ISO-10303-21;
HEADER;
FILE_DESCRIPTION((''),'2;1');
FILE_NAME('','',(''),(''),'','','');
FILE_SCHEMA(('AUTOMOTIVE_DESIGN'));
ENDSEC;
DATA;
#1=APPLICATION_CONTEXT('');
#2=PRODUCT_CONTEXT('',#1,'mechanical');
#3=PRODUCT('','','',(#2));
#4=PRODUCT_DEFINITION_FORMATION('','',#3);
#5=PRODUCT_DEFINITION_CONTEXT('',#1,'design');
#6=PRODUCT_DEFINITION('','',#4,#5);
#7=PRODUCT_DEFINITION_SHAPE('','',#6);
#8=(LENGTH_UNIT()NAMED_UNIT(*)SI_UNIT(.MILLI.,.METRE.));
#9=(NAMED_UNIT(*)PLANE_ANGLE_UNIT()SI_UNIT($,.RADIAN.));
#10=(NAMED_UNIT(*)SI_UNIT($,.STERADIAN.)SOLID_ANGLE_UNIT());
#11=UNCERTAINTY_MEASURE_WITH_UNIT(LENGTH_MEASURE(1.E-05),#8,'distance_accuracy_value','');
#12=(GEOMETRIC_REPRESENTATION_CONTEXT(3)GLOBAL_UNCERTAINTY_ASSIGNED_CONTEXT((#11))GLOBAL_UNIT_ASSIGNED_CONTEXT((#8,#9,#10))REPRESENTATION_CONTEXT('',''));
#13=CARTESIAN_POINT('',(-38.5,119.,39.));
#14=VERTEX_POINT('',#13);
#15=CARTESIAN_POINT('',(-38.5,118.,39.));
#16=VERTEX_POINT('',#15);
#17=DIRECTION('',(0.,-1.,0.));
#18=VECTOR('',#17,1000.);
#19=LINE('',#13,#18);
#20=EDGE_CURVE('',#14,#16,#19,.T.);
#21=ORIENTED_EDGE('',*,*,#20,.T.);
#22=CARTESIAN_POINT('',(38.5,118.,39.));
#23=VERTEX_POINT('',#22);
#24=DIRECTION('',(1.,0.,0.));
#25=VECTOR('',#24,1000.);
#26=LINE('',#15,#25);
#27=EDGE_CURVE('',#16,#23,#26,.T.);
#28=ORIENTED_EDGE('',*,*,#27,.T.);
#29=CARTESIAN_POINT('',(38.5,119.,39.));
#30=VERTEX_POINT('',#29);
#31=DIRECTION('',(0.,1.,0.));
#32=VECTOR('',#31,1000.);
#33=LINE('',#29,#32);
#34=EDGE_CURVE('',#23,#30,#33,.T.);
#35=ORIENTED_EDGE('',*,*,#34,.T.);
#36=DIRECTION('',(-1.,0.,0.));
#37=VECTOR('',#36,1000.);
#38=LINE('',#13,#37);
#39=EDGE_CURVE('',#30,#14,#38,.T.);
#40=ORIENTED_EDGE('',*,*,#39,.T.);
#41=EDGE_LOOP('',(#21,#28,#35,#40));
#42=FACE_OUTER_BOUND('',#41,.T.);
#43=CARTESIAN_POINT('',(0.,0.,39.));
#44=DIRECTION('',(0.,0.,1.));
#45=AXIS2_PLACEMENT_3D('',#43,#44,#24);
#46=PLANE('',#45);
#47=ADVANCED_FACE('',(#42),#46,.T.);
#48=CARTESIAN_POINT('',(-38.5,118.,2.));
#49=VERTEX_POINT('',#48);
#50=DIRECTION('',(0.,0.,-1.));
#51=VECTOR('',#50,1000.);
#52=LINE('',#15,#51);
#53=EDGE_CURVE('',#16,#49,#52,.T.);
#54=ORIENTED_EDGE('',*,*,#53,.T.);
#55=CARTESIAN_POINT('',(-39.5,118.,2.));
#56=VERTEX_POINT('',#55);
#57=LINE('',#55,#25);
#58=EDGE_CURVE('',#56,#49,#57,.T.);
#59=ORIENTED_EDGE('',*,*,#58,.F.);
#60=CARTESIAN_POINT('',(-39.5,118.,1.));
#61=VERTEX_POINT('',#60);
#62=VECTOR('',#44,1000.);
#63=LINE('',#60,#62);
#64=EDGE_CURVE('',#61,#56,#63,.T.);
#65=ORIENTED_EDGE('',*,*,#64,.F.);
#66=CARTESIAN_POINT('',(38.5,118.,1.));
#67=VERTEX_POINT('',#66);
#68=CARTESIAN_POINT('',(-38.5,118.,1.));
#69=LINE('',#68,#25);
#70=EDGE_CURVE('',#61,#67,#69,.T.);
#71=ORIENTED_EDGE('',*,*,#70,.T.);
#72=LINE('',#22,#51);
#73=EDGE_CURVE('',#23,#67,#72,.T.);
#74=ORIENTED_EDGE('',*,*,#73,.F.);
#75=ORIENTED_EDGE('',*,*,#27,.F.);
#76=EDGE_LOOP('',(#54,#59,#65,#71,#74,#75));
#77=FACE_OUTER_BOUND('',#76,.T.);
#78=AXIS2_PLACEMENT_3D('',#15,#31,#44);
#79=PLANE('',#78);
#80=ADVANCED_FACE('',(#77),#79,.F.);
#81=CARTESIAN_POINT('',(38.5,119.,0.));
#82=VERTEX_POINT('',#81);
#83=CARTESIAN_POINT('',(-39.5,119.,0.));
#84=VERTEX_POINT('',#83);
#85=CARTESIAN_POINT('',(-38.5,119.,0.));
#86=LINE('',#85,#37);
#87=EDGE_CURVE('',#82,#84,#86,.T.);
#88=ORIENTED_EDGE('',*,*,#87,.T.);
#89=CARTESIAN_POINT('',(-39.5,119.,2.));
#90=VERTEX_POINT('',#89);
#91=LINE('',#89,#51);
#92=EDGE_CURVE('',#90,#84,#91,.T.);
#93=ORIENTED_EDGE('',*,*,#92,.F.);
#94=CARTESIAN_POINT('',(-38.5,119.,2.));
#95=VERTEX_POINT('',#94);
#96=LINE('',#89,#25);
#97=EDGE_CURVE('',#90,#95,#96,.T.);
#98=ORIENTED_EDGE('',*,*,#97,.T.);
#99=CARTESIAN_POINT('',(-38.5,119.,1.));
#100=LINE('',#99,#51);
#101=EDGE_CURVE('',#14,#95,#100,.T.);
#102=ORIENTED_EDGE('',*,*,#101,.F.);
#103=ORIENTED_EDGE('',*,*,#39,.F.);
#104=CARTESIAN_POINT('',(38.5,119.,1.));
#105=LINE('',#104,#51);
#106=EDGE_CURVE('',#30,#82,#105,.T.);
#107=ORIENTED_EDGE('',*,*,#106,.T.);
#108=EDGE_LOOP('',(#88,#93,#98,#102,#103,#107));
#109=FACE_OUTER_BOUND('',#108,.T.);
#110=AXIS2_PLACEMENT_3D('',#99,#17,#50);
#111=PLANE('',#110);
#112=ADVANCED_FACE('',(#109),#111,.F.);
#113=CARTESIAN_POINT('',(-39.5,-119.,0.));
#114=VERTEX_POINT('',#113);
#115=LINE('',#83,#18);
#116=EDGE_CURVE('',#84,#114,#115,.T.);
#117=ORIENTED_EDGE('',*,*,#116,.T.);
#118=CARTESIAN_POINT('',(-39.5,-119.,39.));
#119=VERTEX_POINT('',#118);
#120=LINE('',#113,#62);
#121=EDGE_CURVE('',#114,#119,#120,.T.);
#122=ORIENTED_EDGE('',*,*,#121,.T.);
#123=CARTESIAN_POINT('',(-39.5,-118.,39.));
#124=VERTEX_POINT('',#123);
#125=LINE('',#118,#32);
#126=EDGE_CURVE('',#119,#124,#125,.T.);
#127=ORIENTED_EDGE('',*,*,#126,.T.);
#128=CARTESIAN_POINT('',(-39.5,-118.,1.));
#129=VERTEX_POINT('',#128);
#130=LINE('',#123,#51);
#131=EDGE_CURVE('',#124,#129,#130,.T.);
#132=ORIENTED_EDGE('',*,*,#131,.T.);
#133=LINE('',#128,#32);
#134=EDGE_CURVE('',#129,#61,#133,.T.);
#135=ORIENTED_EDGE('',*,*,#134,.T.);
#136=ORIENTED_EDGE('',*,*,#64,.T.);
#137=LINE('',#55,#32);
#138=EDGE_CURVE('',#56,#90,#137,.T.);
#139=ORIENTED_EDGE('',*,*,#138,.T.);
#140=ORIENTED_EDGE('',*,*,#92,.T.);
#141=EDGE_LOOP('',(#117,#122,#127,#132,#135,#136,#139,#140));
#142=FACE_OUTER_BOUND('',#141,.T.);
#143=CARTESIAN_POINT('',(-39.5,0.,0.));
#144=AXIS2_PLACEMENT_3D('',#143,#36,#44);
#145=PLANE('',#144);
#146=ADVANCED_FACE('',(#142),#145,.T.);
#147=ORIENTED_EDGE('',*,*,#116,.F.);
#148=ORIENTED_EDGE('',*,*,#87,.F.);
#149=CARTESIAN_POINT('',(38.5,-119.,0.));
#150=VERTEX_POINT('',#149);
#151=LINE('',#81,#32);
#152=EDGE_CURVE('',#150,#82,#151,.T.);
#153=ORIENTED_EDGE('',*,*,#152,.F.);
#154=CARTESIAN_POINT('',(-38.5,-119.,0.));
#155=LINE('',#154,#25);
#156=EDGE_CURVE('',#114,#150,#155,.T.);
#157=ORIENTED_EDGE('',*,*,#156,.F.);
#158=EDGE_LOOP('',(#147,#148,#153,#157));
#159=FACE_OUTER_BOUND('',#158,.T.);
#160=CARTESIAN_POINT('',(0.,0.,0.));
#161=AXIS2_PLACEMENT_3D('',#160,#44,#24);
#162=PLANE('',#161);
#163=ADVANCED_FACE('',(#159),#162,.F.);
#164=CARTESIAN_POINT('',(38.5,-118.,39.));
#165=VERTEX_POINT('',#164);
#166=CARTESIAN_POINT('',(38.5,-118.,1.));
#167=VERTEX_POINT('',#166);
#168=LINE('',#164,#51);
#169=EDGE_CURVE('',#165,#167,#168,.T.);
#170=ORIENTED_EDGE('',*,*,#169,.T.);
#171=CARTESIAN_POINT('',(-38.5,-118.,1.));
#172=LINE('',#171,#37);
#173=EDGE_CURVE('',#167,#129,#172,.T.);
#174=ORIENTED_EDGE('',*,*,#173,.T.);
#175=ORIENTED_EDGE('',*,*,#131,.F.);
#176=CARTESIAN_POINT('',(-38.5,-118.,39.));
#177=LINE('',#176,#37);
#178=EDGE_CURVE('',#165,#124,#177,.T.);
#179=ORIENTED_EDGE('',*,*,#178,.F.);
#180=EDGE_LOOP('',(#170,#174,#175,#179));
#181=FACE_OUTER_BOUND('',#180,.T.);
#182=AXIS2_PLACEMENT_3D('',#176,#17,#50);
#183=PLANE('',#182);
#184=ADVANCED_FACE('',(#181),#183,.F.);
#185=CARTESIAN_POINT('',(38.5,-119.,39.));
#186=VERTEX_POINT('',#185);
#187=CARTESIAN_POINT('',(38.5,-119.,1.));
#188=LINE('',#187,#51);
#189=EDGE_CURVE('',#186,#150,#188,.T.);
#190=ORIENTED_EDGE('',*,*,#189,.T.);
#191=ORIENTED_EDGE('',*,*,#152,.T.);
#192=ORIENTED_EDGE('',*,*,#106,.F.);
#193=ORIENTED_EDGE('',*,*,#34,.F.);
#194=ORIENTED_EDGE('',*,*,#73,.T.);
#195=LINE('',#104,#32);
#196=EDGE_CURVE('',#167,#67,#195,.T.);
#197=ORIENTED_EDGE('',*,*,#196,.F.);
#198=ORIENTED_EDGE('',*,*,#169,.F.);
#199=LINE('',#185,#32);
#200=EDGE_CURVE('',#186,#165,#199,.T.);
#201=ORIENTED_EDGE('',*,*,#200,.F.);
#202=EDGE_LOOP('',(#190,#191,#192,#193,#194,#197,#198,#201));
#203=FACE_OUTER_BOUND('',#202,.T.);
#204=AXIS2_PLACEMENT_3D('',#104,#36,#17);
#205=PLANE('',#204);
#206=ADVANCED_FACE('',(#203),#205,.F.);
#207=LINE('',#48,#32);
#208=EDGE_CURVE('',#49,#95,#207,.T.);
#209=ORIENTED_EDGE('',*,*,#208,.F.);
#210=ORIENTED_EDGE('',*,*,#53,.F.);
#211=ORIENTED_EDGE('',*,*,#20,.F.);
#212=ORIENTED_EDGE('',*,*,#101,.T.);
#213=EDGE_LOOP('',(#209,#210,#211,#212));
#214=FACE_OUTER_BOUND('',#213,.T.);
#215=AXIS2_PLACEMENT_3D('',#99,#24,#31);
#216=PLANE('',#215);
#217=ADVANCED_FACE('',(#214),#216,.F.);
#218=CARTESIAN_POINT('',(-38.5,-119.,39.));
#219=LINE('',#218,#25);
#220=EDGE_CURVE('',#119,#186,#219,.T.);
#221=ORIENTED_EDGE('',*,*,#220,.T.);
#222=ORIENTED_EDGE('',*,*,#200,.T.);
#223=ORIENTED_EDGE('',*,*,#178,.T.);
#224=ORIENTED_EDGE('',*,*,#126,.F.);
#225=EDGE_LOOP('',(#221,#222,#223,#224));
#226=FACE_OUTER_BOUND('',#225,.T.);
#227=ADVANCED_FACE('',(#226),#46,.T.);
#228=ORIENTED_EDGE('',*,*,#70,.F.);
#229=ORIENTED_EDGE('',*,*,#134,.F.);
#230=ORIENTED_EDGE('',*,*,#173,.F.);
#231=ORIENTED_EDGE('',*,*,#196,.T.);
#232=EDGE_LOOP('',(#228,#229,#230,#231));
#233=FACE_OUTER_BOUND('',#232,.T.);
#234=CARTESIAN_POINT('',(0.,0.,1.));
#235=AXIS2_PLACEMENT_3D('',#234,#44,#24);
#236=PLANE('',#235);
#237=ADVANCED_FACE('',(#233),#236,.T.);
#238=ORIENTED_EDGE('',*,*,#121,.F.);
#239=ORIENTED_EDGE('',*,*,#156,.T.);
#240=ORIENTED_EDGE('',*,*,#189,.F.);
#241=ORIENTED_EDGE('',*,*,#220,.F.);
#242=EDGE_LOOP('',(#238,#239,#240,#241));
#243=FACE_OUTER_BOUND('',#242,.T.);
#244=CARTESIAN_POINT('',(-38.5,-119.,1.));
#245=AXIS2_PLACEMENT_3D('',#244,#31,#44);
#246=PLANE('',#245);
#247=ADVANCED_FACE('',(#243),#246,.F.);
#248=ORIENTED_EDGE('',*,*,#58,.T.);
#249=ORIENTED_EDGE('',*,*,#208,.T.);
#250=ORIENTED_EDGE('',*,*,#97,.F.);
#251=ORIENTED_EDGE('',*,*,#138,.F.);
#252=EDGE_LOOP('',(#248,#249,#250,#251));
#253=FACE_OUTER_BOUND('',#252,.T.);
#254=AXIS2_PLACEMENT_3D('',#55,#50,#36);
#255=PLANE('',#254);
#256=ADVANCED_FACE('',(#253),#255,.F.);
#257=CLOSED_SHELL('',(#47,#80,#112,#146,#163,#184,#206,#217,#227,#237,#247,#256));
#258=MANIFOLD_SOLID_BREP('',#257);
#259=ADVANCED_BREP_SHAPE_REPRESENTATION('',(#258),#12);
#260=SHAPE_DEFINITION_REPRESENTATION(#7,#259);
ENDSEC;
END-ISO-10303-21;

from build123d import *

# Parameters (mm, degrees)
SKETCH1_W           = 77
SKETCH1_H           = 238
BOSS_EXTRUDE1_DEPTH = 1
SKETCH2_W           = 77
SKETCH2_H           = 1
BOSS_EXTRUDE2_DEPTH = 38
BOSS_EXTRUDE3_DEPTH = 1


with BuildPart() as part:
    # Sketch1 → Boss-Extrude1 (new body)
    with BuildSketch(Plane.XY):
        Rectangle(SKETCH1_W, SKETCH1_H)
    extrude(amount=BOSS_EXTRUDE1_DEPTH)

    # Sketch2 → Boss-Extrude2 (add)
    with BuildSketch(Plane.XY.offset(1)):
        with Locations((0, 118.5)):
            Rectangle(SKETCH2_W, SKETCH2_H)
        with Locations((0, -118.5)):
            Rectangle(SKETCH2_W, SKETCH2_H)
    extrude(amount=BOSS_EXTRUDE2_DEPTH)

    # Sketch3 → Boss-Extrude3 (add)
    with BuildSketch(Plane.ZY.offset(38.5)):
        Polygon((2, 119), (0, 119), (0, -119), (39, -119), (39, -118), (1, -118), (1, 118), (2, 118), align=None)
    extrude(amount=BOSS_EXTRUDE3_DEPTH)


solid = part.part
